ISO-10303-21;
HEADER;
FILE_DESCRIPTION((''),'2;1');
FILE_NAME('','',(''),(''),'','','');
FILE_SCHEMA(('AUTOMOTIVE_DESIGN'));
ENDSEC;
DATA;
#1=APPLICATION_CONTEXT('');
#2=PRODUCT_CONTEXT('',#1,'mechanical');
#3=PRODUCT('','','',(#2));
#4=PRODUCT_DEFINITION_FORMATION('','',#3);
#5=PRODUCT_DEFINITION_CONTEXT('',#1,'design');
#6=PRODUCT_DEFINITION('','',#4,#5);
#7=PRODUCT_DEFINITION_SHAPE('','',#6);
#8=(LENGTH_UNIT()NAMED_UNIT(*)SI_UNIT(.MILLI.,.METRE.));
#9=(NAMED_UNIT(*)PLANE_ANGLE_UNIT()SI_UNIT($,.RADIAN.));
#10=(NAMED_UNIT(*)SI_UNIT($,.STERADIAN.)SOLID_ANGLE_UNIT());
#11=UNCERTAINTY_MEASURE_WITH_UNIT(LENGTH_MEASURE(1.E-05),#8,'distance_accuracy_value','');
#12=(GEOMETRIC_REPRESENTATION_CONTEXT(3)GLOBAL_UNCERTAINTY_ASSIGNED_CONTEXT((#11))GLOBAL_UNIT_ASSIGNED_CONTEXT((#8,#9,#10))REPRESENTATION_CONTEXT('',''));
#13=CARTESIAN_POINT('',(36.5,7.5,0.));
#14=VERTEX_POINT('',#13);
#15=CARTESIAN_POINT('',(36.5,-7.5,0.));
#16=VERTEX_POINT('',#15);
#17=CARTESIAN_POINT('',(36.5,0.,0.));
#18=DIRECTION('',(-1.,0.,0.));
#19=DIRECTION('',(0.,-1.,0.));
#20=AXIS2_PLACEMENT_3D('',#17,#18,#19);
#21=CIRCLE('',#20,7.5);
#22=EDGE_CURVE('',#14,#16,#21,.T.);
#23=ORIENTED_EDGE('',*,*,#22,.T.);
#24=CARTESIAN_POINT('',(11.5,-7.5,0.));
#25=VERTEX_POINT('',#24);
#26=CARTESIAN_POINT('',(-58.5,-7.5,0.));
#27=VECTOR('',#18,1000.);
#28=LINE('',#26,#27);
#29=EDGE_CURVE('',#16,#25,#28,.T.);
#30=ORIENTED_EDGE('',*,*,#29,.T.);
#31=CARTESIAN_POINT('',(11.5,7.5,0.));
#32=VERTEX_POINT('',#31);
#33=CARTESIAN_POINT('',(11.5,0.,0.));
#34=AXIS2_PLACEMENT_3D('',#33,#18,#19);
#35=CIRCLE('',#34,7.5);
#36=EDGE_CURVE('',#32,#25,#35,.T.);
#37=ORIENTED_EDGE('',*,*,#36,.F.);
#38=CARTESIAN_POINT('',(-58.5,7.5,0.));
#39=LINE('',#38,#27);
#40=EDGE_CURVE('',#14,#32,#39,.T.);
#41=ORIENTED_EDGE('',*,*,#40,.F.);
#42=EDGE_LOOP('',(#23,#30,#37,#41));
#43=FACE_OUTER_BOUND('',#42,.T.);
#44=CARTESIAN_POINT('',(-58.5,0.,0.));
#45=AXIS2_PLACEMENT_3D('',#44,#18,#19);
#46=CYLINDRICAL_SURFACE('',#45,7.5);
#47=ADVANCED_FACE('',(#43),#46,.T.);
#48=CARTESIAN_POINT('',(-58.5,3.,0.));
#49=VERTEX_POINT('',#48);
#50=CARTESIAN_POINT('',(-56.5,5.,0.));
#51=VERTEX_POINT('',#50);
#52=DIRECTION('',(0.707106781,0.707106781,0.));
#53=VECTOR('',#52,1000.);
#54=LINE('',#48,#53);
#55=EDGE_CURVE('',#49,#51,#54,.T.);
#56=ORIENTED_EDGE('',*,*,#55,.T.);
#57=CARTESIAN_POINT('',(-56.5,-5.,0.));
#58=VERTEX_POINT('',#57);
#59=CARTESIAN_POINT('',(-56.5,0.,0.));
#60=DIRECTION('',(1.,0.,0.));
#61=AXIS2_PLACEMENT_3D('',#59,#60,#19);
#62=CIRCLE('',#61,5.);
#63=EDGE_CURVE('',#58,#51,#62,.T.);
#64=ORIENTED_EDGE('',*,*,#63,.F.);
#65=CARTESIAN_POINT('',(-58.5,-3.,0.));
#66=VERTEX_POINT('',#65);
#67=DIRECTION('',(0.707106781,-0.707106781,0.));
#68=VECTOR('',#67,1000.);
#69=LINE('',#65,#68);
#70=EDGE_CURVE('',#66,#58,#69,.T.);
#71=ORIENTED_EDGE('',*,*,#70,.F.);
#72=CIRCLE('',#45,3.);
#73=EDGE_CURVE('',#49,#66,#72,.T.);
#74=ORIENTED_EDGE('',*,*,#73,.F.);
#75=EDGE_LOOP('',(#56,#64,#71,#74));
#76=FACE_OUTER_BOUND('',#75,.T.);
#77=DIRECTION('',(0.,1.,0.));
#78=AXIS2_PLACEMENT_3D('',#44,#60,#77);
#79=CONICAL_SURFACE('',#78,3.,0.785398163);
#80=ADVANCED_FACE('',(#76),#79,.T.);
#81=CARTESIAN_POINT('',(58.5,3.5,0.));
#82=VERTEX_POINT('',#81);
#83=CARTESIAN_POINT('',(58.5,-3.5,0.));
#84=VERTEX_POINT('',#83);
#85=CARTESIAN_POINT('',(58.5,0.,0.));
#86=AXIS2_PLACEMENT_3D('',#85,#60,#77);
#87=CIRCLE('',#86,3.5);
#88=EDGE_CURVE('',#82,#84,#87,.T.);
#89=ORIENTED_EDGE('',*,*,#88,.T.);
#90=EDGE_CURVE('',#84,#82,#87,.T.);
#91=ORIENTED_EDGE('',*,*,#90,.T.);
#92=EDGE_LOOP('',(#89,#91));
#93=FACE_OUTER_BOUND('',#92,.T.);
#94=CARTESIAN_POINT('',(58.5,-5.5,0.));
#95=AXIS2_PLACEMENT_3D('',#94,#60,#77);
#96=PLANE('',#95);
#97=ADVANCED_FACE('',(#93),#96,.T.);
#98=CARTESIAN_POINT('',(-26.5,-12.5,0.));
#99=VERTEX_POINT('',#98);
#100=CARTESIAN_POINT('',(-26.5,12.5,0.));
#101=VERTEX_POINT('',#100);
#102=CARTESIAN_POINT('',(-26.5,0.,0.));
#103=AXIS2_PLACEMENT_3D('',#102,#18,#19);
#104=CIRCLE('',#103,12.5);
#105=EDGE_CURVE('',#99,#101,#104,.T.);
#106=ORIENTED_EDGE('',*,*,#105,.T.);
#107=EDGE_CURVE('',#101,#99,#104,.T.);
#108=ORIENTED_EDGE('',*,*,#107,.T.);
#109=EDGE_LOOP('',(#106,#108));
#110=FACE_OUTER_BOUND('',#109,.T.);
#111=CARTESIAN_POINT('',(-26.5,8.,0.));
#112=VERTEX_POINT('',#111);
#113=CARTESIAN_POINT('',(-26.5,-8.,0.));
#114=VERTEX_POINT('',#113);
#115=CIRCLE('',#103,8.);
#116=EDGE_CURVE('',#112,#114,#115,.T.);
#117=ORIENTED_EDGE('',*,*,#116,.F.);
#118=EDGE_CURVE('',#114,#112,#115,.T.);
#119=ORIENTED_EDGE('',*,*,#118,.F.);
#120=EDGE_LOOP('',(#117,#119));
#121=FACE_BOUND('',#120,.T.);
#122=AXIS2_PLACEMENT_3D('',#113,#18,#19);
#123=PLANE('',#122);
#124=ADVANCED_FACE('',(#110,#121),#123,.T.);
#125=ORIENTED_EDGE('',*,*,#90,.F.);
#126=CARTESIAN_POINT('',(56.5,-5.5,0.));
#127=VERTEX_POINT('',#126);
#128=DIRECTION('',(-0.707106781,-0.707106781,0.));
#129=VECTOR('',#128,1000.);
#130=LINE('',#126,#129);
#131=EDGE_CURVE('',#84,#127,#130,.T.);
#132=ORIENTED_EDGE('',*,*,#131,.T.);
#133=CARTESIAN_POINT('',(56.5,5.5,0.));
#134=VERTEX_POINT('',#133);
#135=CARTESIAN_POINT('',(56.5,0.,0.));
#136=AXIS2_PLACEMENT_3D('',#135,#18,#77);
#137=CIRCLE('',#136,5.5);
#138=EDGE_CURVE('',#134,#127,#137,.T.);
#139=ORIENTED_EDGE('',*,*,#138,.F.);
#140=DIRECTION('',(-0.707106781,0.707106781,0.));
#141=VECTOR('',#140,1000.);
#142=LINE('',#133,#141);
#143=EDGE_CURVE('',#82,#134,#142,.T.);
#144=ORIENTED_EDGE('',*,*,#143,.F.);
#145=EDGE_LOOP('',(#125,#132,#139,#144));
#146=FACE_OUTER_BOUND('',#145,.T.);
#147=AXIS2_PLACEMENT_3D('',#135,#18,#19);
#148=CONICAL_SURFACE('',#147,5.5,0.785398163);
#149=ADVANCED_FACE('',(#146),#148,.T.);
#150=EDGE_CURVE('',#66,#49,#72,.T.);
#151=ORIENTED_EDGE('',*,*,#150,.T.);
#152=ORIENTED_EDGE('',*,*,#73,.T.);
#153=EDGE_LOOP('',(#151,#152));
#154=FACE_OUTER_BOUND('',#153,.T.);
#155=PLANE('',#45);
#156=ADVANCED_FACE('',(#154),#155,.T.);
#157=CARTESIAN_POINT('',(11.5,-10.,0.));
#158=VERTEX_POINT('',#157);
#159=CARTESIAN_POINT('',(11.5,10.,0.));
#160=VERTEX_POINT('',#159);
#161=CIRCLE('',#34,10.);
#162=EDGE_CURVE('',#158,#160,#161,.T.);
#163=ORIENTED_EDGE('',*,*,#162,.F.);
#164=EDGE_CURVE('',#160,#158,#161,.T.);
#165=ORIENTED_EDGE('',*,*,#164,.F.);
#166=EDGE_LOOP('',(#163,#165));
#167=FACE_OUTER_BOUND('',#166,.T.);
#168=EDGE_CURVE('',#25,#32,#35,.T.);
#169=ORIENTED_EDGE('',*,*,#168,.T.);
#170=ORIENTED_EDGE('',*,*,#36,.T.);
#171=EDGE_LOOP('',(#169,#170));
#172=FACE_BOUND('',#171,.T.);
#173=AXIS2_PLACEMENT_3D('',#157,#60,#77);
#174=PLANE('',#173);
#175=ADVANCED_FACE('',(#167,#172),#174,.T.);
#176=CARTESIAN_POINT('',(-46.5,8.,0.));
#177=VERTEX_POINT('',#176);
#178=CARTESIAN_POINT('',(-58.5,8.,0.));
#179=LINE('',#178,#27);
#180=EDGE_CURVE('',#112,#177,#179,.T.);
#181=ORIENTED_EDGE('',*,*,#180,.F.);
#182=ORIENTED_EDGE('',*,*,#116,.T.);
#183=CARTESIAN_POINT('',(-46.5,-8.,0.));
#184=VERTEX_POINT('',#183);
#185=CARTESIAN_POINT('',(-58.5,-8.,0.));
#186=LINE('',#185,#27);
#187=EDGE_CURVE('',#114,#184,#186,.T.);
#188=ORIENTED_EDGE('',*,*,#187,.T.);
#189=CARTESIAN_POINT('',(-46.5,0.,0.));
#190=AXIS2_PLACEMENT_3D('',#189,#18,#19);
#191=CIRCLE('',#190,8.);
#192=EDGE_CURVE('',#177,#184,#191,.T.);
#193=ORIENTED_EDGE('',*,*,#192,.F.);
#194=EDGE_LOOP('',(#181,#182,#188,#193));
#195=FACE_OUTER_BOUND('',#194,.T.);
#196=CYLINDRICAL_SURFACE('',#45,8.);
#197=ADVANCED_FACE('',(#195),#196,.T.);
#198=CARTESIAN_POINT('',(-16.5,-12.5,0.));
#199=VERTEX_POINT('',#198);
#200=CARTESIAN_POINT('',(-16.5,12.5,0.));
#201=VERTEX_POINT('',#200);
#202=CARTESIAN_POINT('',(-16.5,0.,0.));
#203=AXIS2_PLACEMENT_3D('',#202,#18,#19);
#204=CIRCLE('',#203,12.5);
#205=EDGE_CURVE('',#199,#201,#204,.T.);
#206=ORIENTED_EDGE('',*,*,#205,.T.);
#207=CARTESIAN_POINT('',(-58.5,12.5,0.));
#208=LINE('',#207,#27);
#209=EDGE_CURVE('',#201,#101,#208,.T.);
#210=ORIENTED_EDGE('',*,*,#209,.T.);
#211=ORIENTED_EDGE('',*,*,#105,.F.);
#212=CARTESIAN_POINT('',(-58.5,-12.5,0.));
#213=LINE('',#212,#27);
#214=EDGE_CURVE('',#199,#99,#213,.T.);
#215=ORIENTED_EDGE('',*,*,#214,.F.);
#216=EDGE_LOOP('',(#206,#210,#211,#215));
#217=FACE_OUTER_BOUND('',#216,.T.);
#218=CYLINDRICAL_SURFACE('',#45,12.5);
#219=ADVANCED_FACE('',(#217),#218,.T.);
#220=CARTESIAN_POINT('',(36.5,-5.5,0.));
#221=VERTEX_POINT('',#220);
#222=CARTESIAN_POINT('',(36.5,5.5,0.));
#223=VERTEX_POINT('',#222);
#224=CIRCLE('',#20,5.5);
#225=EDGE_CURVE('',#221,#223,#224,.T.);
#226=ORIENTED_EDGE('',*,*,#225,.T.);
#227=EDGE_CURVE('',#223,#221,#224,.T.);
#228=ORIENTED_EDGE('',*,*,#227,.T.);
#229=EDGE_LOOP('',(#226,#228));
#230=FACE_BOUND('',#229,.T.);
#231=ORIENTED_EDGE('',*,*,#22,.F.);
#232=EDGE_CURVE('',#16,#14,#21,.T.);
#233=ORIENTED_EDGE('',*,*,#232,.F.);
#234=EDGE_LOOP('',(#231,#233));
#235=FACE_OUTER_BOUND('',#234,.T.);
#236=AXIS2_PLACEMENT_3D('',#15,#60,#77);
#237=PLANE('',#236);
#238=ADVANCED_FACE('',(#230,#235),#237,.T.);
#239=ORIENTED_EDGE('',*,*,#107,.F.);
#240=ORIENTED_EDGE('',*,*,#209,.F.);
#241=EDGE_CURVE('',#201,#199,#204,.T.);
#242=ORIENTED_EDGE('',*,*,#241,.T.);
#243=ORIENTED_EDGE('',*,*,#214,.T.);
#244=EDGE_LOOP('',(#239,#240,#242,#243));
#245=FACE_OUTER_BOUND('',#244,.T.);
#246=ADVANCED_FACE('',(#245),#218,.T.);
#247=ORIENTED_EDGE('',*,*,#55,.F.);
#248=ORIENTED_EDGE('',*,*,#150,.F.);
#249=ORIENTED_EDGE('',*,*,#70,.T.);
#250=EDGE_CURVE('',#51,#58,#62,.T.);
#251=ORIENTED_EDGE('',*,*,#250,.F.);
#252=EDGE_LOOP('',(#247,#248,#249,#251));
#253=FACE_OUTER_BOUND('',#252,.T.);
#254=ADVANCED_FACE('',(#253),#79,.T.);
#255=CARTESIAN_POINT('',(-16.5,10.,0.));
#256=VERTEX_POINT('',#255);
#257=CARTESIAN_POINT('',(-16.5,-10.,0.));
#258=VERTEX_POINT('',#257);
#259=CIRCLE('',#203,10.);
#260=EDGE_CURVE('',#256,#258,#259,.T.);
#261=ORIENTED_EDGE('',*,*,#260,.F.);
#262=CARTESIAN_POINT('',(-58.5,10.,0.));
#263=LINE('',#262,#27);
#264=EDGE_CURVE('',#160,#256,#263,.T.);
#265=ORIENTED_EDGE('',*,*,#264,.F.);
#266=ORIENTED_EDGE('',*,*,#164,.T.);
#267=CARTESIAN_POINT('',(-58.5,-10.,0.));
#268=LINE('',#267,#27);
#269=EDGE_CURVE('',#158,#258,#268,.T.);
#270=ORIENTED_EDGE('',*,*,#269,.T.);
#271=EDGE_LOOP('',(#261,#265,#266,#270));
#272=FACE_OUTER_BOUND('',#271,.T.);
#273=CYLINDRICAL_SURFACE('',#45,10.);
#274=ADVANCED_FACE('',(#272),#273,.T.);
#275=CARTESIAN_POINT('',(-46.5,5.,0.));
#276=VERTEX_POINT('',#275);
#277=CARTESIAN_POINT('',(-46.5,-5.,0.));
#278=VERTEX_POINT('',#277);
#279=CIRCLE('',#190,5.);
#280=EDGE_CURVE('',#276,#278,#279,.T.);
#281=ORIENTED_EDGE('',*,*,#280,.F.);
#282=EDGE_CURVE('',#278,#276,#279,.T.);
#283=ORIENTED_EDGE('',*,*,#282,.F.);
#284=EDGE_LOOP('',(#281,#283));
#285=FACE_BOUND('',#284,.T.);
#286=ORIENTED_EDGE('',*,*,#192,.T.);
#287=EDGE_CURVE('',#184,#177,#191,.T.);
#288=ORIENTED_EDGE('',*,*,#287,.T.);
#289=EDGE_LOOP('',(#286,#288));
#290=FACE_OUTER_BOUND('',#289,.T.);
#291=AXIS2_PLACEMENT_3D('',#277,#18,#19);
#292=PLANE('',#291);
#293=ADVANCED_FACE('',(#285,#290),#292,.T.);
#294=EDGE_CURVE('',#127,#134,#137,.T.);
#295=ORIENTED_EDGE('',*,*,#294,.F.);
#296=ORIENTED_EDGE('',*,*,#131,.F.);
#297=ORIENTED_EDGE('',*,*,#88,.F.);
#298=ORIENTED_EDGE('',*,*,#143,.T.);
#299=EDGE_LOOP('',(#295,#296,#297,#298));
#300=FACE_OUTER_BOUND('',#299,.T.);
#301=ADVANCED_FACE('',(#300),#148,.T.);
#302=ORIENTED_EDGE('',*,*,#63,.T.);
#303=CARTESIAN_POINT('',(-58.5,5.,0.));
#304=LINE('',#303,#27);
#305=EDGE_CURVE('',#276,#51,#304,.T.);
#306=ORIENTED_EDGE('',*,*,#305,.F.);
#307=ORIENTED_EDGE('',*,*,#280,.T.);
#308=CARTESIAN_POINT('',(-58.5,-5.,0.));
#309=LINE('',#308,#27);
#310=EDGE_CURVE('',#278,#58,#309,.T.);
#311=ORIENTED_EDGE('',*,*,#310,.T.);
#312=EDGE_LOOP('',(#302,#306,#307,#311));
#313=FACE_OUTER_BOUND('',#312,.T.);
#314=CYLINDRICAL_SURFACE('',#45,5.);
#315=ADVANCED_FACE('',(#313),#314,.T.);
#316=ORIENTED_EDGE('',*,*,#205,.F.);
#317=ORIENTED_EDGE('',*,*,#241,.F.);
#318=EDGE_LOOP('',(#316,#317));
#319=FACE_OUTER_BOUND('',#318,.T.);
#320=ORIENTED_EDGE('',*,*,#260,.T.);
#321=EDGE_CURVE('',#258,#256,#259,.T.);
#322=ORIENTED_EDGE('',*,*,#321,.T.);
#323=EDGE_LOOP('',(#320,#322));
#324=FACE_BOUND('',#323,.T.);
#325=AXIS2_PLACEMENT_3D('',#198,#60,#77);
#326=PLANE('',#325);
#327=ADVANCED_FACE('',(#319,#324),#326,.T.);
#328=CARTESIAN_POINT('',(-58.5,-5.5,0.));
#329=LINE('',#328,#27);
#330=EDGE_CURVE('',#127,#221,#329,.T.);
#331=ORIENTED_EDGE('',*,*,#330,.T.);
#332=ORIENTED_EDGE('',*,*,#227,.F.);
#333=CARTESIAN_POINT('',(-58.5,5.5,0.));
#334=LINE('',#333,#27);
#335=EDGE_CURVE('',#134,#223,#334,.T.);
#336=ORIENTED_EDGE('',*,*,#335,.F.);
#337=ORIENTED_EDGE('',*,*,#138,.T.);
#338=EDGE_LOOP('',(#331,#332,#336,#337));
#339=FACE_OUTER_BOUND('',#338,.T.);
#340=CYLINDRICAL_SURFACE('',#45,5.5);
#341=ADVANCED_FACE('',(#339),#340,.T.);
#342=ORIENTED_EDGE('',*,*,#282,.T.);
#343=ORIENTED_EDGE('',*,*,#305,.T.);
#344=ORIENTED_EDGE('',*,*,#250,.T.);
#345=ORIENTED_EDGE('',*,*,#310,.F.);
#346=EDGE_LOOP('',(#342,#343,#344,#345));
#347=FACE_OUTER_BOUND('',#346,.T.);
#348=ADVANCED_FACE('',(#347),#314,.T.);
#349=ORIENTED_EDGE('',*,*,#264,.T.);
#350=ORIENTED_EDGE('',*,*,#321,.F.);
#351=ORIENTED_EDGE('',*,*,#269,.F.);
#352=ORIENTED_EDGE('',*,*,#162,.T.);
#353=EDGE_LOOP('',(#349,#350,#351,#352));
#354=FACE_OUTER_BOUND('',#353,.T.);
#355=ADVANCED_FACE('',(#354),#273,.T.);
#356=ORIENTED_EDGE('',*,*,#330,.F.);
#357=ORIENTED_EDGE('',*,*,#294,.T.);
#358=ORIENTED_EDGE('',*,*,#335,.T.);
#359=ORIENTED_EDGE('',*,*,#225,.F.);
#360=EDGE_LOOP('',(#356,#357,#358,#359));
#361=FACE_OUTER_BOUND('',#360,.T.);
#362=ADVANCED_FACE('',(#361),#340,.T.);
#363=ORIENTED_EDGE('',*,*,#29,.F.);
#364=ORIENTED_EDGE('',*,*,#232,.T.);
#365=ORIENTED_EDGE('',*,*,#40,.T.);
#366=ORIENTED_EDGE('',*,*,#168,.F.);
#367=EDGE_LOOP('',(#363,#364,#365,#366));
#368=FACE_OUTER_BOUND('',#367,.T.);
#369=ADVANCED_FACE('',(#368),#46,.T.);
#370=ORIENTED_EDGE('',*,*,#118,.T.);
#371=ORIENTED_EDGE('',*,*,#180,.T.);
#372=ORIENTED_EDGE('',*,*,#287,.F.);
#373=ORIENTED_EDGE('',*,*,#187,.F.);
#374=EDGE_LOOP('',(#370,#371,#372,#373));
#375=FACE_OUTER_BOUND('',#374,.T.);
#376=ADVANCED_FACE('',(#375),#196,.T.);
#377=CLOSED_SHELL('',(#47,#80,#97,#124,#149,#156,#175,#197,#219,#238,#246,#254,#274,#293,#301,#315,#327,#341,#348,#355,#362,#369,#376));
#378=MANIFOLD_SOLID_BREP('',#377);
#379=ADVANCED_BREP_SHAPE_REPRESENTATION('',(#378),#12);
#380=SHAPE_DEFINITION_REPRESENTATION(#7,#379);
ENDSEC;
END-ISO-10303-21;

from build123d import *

# Parameters (mm, degrees)
EDGE_CHAMFER_2X45_SIZE = 2


with BuildPart() as part:
    # Shaft Profile Sketch → Stepped Shaft Revolve (revolve)
    with BuildSketch(Plane.XY):
        Polygon((-58.5, 0), (-58.5, -5), (-46.5, -5), (-46.5, -8), (-26.5, -8), (-26.5, -12.5), (-16.5, -12.5), (-16.5, -10), (11.5, -10), (11.5, -7.5), (36.5, -7.5), (36.5, -5.5), (58.5, -5.5), (58.5, 0), align=None)
    revolve(axis=Axis((-58.5, 0, 0), (1, 0, 0)))

    # Edge Chamfer 2x45°
    edge_chamfer_2x45_edges = [part.edges().sort_by_distance(p)[0] for p in [
        (58.5, 5.5, 0),
        (-58.5, 5, 0),
    ]]
    chamfer(edge_chamfer_2x45_edges, length=EDGE_CHAMFER_2X45_SIZE)


solid = part.part
